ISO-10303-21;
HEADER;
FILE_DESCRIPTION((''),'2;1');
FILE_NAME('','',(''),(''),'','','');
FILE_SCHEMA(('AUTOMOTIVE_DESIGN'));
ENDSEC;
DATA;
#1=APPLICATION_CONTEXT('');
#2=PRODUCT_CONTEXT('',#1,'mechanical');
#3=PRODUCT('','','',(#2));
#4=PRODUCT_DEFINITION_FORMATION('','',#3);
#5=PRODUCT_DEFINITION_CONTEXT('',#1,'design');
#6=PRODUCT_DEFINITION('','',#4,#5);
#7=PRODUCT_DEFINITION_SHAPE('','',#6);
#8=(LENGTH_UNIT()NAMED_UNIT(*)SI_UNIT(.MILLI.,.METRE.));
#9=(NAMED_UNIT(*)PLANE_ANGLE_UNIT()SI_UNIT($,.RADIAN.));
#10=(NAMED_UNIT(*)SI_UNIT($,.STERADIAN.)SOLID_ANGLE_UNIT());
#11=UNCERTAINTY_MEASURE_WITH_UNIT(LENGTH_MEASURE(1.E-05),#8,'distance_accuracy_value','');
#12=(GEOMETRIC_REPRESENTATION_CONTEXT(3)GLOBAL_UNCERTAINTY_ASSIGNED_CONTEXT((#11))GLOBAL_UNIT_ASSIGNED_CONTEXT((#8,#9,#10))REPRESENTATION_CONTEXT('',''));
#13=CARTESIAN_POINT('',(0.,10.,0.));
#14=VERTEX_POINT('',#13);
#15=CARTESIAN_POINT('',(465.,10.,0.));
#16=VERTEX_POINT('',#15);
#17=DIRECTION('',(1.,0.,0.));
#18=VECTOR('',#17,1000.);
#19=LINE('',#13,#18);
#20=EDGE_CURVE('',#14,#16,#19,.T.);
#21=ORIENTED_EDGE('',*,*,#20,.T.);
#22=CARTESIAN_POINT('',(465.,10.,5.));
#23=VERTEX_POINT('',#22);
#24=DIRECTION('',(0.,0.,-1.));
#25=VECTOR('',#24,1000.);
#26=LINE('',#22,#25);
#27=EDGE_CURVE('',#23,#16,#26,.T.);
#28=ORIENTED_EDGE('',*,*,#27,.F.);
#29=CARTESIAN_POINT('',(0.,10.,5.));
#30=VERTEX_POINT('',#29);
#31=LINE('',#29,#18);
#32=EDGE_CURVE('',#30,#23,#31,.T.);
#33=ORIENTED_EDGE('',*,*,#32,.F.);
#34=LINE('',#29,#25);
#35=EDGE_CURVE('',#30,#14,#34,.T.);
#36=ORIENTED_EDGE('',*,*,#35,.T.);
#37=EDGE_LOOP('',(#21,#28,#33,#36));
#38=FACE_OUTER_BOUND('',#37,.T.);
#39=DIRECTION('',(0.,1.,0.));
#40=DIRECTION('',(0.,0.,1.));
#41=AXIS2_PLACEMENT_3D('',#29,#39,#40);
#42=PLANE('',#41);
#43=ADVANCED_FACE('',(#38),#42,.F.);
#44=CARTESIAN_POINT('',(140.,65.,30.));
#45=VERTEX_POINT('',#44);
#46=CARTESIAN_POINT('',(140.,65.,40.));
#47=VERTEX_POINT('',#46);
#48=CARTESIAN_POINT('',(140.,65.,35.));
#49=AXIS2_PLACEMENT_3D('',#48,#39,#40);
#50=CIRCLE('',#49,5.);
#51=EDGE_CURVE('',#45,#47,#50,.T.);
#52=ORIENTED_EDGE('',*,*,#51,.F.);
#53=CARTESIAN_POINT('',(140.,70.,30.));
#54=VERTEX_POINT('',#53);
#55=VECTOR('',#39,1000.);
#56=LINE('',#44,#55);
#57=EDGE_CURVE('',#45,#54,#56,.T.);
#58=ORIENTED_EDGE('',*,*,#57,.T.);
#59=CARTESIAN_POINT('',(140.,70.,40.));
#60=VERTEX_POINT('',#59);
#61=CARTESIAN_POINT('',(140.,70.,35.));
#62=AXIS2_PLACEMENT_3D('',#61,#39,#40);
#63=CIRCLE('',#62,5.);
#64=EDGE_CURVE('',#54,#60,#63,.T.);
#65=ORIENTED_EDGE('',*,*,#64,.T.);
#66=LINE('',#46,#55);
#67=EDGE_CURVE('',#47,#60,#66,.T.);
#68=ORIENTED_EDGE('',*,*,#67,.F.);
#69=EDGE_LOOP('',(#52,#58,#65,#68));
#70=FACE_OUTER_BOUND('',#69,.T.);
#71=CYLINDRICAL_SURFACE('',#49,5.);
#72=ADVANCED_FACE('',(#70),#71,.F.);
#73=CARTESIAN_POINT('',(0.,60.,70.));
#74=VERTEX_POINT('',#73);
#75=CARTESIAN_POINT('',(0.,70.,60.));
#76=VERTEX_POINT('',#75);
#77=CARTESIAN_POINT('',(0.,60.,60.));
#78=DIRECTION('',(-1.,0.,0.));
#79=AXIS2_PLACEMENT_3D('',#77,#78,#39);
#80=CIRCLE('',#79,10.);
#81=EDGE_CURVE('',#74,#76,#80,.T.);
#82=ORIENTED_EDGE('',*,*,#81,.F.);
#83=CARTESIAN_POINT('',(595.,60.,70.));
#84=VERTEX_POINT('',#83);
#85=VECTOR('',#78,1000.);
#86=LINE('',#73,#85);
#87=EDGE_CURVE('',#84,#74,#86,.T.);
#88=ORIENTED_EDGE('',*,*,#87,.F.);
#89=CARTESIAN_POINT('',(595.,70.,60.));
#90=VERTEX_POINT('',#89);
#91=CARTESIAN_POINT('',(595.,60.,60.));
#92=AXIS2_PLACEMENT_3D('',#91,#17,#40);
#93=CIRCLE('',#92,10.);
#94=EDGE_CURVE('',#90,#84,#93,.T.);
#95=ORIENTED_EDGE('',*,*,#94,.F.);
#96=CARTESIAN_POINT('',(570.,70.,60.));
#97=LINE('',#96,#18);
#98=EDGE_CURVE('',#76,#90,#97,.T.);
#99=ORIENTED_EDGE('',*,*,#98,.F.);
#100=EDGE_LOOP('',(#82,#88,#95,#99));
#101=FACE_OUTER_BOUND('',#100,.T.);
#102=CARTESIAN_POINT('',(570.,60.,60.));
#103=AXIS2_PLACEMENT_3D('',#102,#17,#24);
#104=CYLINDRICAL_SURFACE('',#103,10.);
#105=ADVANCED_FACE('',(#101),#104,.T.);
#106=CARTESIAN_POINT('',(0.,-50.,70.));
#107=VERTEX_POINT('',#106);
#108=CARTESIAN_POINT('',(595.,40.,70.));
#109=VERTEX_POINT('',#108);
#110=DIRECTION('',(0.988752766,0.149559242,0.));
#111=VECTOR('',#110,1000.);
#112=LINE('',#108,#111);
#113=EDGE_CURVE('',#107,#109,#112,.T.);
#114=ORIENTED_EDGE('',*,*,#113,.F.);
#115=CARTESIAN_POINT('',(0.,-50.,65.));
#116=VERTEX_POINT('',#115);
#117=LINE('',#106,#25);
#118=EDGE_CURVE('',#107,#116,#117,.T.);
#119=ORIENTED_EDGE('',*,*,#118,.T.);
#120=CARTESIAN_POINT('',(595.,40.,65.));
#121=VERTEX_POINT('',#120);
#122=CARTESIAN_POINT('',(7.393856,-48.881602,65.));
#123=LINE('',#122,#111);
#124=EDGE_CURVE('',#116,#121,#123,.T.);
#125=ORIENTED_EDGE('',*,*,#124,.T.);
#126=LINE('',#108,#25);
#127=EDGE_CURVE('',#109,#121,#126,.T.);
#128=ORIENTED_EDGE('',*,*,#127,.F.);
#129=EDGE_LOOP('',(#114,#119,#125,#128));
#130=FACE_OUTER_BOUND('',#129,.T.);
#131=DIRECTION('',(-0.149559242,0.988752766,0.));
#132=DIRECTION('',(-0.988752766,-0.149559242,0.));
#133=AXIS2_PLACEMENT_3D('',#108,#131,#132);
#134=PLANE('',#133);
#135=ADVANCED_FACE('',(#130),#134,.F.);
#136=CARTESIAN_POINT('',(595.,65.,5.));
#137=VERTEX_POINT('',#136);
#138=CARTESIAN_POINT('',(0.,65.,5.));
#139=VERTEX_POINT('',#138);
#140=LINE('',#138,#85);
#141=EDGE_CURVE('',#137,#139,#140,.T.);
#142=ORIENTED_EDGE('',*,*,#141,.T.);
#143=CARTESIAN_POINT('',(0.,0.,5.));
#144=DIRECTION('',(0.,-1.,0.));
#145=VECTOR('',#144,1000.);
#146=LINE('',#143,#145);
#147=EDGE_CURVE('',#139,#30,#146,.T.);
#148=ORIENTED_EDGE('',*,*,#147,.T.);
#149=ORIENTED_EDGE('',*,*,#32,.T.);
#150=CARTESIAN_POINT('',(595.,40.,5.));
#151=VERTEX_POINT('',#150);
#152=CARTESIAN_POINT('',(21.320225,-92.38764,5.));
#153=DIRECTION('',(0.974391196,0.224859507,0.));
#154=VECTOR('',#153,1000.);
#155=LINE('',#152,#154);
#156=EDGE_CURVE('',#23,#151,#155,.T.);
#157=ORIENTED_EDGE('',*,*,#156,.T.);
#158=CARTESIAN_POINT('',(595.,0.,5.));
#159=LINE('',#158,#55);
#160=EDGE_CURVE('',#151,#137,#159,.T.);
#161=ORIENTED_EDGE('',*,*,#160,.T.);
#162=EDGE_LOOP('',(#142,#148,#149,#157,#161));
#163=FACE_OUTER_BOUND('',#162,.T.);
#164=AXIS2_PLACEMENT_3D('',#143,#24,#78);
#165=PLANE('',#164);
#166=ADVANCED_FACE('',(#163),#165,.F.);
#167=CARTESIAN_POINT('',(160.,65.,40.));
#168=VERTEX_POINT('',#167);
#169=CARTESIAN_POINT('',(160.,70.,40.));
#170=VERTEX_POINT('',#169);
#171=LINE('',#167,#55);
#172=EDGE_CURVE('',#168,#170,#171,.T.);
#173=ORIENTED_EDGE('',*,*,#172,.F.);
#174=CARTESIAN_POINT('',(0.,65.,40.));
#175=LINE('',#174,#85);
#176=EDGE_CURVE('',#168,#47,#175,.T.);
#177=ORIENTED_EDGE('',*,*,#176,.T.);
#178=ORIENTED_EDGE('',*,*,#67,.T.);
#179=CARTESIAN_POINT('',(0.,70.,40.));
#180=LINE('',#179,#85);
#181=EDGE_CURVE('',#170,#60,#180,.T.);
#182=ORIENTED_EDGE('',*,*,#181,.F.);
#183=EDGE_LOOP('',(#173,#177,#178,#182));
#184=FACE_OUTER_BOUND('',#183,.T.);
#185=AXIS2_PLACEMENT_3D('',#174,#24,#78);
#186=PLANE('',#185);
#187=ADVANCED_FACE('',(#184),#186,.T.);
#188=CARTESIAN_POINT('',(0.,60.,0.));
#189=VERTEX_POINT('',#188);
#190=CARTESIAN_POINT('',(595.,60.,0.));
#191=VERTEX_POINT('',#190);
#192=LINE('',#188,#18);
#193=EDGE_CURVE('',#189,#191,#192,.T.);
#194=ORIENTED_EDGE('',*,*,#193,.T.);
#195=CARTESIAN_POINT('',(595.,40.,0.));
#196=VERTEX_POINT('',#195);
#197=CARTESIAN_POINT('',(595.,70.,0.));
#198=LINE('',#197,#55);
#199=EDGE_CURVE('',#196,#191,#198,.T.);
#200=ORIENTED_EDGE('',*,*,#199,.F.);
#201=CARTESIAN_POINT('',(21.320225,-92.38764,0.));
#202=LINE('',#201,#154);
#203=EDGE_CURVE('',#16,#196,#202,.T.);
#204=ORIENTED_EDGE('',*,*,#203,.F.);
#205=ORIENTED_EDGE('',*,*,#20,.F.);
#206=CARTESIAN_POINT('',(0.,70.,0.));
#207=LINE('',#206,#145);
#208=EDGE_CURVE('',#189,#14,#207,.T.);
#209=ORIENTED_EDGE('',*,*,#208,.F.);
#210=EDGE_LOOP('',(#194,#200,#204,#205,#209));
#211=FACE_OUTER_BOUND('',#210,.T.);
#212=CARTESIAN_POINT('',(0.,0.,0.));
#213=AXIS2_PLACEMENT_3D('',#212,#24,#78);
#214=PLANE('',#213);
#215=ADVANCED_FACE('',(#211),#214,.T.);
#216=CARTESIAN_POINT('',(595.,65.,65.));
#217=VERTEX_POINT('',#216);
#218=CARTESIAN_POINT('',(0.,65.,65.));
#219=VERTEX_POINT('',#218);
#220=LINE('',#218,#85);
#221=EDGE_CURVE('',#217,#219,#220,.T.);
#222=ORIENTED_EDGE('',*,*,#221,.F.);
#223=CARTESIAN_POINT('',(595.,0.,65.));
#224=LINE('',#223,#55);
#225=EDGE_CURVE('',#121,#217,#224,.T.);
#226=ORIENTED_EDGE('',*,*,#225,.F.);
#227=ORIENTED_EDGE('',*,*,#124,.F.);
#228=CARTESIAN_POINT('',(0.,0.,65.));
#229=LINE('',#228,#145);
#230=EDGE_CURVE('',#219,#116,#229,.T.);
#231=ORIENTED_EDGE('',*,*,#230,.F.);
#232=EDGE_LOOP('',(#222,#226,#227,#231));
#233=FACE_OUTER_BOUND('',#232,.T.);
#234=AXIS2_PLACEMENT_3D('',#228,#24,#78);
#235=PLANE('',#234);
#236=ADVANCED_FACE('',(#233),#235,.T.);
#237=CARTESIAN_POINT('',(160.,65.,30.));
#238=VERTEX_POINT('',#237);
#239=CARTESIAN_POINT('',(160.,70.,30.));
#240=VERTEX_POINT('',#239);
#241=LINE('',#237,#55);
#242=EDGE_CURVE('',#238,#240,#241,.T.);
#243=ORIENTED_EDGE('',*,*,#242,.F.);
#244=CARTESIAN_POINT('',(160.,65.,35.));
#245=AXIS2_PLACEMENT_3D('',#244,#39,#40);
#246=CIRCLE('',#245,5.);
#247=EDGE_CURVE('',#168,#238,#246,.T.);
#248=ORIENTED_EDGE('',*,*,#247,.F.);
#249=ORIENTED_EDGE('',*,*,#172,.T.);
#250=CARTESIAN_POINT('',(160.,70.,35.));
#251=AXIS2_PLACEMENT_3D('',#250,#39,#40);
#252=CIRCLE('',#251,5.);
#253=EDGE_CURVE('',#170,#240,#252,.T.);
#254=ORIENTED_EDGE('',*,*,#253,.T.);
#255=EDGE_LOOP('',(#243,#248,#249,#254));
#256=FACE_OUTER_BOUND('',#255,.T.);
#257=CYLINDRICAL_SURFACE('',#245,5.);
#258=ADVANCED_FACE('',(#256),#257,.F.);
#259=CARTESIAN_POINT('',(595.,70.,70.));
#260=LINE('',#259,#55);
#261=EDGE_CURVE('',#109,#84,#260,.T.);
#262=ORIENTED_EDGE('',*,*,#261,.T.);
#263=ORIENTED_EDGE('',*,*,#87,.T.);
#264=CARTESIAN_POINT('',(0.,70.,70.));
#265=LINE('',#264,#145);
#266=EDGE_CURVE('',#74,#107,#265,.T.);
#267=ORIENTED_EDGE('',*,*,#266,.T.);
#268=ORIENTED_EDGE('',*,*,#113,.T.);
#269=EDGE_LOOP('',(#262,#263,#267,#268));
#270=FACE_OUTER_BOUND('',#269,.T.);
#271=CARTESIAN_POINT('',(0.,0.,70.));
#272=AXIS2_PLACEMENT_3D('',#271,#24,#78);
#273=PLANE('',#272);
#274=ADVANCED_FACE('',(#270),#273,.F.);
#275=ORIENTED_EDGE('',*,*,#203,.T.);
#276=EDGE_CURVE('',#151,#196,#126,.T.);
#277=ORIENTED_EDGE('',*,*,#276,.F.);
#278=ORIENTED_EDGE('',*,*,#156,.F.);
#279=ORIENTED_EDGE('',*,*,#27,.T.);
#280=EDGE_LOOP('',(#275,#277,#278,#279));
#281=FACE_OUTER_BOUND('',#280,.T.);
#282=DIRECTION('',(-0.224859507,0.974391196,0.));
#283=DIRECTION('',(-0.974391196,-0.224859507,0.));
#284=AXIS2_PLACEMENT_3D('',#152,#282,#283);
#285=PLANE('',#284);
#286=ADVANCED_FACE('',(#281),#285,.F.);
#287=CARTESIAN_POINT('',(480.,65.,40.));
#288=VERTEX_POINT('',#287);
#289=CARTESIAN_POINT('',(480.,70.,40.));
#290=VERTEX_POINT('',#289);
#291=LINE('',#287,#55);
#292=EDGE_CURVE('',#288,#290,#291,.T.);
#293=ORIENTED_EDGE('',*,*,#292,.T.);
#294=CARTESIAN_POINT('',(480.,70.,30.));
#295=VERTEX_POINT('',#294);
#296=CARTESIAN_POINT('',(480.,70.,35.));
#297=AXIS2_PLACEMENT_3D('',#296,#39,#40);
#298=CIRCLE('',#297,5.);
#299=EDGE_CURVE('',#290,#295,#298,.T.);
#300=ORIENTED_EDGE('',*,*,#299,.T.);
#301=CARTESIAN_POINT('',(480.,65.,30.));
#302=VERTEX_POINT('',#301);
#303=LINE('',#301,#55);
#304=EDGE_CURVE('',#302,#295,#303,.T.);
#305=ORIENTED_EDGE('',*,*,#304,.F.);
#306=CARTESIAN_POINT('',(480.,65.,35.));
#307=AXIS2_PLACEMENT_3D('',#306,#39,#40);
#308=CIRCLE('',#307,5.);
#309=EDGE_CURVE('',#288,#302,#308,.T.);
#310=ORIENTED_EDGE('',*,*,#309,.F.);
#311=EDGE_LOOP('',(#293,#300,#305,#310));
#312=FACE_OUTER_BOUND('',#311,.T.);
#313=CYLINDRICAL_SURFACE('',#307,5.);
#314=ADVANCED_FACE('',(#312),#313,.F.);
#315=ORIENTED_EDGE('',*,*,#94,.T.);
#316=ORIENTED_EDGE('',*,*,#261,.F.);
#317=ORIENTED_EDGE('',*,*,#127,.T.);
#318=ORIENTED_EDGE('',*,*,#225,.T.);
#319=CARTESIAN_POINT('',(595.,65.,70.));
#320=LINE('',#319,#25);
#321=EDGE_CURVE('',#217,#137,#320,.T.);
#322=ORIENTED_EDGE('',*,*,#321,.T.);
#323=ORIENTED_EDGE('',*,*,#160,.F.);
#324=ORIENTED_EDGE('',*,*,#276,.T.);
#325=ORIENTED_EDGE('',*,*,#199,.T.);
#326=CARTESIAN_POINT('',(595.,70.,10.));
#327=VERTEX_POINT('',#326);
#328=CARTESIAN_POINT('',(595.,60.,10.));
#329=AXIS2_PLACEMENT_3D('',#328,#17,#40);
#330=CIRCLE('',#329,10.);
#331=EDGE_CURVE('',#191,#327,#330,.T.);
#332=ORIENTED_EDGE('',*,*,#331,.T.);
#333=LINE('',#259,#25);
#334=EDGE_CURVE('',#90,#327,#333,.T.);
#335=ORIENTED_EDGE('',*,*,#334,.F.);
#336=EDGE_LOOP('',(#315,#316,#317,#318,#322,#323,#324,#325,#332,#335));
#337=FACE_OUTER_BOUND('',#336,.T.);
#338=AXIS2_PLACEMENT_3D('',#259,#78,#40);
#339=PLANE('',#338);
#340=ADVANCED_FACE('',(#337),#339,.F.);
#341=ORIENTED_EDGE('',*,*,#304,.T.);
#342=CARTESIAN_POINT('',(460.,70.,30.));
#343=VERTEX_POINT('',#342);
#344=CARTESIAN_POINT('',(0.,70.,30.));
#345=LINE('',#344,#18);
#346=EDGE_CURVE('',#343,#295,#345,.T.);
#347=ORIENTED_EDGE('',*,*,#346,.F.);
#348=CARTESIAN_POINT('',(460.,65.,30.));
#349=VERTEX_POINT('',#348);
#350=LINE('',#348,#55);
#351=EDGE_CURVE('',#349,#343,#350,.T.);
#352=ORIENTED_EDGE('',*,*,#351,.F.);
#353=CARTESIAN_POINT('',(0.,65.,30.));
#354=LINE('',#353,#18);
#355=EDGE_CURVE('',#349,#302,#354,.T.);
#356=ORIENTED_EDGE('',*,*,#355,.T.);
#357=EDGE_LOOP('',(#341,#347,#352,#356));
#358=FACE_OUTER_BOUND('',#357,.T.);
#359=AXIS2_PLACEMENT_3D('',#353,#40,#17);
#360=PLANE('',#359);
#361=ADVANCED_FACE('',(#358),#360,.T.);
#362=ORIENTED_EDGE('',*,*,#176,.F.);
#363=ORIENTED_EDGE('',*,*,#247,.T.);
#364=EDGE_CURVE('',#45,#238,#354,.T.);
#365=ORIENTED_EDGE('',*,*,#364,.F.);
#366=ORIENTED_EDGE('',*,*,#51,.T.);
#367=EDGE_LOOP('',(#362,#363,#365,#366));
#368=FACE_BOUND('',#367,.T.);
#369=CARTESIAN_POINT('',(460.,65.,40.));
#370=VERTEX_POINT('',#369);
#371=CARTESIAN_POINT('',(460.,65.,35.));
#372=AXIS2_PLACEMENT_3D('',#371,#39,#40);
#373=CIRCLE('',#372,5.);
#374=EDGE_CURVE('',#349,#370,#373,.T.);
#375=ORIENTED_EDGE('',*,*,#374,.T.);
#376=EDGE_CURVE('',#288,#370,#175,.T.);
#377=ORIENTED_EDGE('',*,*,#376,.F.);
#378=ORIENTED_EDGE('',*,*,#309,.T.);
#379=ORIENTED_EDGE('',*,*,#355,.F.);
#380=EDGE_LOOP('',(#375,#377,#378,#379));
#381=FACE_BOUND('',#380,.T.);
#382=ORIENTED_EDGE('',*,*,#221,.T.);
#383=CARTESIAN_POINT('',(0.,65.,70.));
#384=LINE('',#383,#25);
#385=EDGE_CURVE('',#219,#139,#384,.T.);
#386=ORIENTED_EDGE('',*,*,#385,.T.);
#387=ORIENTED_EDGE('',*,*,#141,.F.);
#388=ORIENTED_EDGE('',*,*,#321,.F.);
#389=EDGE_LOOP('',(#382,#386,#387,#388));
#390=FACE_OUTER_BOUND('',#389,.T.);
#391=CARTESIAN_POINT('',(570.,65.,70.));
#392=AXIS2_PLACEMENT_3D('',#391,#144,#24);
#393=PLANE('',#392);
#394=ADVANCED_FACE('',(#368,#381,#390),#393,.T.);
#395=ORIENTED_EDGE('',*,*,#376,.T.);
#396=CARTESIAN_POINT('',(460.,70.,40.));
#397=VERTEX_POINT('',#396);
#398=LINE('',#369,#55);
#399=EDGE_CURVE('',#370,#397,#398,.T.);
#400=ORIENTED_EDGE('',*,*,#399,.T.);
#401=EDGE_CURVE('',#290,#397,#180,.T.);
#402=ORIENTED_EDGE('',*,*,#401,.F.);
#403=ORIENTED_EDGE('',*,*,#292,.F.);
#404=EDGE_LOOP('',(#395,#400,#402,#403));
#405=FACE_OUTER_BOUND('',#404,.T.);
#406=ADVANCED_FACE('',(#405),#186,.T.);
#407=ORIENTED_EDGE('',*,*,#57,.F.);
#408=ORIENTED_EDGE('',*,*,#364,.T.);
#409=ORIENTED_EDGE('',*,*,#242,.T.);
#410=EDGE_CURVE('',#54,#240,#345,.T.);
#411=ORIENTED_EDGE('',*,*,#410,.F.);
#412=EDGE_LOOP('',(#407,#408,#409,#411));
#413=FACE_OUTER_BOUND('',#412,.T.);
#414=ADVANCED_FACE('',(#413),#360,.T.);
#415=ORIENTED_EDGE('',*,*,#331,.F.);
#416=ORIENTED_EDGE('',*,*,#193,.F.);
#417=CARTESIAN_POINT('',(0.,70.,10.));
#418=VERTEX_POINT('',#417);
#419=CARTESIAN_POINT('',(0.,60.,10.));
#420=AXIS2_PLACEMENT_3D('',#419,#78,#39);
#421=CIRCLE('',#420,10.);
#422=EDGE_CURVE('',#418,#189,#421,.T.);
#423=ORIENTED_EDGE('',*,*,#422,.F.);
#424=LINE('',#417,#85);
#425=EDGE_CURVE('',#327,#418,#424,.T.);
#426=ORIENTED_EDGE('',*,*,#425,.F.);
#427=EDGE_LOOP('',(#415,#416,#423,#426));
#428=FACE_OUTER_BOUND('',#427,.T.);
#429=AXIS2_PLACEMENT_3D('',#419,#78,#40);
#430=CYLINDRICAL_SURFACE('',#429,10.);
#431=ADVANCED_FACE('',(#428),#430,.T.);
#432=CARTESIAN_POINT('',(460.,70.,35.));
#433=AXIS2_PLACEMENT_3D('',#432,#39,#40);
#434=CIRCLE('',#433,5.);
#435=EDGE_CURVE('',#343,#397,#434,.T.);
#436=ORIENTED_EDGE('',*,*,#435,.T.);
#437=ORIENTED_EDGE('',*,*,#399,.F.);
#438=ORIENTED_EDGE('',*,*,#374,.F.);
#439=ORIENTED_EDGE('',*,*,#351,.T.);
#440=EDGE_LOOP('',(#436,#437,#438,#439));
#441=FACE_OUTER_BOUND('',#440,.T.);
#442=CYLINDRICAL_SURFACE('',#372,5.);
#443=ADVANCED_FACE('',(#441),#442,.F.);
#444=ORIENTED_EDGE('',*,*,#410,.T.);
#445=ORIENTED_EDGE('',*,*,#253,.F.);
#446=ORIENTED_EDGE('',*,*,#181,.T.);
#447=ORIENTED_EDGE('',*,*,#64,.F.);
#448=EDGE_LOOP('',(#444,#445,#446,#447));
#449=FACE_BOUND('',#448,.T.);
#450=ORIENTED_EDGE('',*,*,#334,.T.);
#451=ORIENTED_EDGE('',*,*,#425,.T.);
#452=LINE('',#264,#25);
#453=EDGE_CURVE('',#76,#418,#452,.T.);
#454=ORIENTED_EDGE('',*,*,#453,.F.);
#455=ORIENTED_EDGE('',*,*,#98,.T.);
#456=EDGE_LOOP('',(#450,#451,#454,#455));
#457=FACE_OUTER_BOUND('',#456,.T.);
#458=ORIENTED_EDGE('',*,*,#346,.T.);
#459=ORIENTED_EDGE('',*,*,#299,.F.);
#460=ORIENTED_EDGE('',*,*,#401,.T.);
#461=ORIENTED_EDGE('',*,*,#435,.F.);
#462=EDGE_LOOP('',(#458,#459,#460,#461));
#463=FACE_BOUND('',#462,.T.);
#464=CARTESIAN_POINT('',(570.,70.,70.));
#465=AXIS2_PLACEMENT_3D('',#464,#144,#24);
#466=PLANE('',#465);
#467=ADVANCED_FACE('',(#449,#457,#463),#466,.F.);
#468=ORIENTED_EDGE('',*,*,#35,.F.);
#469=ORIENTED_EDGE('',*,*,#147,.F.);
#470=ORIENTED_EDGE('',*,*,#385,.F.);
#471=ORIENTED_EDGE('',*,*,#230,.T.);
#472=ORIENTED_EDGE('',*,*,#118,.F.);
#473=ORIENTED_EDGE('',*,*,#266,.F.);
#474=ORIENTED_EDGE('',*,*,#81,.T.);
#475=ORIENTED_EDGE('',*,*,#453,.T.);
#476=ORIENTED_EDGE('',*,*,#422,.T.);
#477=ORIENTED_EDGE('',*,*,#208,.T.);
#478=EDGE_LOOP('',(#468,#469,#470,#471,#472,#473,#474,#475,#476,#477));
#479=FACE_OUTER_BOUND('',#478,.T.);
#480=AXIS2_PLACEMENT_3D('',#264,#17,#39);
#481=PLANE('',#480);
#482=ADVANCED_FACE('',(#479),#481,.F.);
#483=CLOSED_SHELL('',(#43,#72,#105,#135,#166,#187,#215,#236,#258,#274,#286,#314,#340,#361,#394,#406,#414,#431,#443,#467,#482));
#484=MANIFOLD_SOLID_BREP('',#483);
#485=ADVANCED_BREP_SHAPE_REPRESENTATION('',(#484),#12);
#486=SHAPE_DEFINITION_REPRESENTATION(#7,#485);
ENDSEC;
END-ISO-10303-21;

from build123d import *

# Parameters (mm, degrees)
EXTRUDE_1_DEPTH     = 70
SHELL_1_T           = -5
EXTRUDE_2_DEPTH     = 5
CUT_EXTRUDE_1_DEPTH = 5
FILLET_1_R          = 10
FILLET_2_R          = 10
CUT_EXTRUDE_2_DEPTH = 5


with BuildPart() as part:
    # 草图1 → 凸台-拉伸1 (new body)
    with BuildSketch(Plane.XY):
        Polygon((0, 70), (0, -50), (595, 40), (595, 70), (570, 70), align=None)
    extrude(amount=EXTRUDE_1_DEPTH)

    # 抽壳1
    shell_1_openings = [part.faces().sort_by_distance(p)[0] for p in [
        (0, 10, 35),
        (595, 55, 35),
        (297.5, -5, 35),
    ]]
    offset(amount=SHELL_1_T, openings=shell_1_openings, kind=Kind.INTERSECTION)

    # 草图2 → 凸台-拉伸2 (add)
    with BuildSketch(Plane(origin=(0, 0, 0), x_dir=(-1, 0, 0), z_dir=(0, 0, -1))):
        Polygon((-396.666666667, 10), (-595, 40), (-465, 10), align=None)
    extrude(amount=-EXTRUDE_2_DEPTH)

    # 草图3 → 切除-拉伸1 (cut)
    with BuildSketch(Plane(origin=(0, 0, 0), x_dir=(-1, 0, 0), z_dir=(0, 0, -1))):
        Polygon((0, 10), (-396.666666667, 10), (0, -50), align=None)
    extrude(amount=-CUT_EXTRUDE_1_DEPTH, mode=Mode.SUBTRACT)

    # 圆角1
    fillet_1_edges = [part.edges().sort_by_distance(p)[0] for p in [
        (297.5, 70, 0),
    ]]
    fillet(fillet_1_edges, radius=FILLET_1_R)

    # 圆角2
    fillet_2_edges = [part.edges().sort_by_distance(p)[0] for p in [
        (297.5, 70, 70),
    ]]
    fillet(fillet_2_edges, radius=FILLET_2_R)

    # 草图4 → 切除-拉伸2 (cut)
    with BuildSketch(Plane(origin=(0, 70, 0), x_dir=(1, 0, 0), z_dir=(0, 1, 0))):
        with BuildLine():
            Line((460, -30), (480, -30))
            ThreePointArc((480, -30), (485, -35), (480, -40))
            Line((480, -40), (460, -40))
            ThreePointArc((460, -40), (455, -35), (460, -30))
        make_face()
        with BuildLine():
            Line((160, -40), (140, -40))
            ThreePointArc((140, -40), (135, -35), (140, -30))
            Line((140, -30), (160, -30))
            ThreePointArc((160, -30), (165, -35), (160, -40))
        make_face()
    extrude(amount=-CUT_EXTRUDE_2_DEPTH, mode=Mode.SUBTRACT)


solid = part.part
